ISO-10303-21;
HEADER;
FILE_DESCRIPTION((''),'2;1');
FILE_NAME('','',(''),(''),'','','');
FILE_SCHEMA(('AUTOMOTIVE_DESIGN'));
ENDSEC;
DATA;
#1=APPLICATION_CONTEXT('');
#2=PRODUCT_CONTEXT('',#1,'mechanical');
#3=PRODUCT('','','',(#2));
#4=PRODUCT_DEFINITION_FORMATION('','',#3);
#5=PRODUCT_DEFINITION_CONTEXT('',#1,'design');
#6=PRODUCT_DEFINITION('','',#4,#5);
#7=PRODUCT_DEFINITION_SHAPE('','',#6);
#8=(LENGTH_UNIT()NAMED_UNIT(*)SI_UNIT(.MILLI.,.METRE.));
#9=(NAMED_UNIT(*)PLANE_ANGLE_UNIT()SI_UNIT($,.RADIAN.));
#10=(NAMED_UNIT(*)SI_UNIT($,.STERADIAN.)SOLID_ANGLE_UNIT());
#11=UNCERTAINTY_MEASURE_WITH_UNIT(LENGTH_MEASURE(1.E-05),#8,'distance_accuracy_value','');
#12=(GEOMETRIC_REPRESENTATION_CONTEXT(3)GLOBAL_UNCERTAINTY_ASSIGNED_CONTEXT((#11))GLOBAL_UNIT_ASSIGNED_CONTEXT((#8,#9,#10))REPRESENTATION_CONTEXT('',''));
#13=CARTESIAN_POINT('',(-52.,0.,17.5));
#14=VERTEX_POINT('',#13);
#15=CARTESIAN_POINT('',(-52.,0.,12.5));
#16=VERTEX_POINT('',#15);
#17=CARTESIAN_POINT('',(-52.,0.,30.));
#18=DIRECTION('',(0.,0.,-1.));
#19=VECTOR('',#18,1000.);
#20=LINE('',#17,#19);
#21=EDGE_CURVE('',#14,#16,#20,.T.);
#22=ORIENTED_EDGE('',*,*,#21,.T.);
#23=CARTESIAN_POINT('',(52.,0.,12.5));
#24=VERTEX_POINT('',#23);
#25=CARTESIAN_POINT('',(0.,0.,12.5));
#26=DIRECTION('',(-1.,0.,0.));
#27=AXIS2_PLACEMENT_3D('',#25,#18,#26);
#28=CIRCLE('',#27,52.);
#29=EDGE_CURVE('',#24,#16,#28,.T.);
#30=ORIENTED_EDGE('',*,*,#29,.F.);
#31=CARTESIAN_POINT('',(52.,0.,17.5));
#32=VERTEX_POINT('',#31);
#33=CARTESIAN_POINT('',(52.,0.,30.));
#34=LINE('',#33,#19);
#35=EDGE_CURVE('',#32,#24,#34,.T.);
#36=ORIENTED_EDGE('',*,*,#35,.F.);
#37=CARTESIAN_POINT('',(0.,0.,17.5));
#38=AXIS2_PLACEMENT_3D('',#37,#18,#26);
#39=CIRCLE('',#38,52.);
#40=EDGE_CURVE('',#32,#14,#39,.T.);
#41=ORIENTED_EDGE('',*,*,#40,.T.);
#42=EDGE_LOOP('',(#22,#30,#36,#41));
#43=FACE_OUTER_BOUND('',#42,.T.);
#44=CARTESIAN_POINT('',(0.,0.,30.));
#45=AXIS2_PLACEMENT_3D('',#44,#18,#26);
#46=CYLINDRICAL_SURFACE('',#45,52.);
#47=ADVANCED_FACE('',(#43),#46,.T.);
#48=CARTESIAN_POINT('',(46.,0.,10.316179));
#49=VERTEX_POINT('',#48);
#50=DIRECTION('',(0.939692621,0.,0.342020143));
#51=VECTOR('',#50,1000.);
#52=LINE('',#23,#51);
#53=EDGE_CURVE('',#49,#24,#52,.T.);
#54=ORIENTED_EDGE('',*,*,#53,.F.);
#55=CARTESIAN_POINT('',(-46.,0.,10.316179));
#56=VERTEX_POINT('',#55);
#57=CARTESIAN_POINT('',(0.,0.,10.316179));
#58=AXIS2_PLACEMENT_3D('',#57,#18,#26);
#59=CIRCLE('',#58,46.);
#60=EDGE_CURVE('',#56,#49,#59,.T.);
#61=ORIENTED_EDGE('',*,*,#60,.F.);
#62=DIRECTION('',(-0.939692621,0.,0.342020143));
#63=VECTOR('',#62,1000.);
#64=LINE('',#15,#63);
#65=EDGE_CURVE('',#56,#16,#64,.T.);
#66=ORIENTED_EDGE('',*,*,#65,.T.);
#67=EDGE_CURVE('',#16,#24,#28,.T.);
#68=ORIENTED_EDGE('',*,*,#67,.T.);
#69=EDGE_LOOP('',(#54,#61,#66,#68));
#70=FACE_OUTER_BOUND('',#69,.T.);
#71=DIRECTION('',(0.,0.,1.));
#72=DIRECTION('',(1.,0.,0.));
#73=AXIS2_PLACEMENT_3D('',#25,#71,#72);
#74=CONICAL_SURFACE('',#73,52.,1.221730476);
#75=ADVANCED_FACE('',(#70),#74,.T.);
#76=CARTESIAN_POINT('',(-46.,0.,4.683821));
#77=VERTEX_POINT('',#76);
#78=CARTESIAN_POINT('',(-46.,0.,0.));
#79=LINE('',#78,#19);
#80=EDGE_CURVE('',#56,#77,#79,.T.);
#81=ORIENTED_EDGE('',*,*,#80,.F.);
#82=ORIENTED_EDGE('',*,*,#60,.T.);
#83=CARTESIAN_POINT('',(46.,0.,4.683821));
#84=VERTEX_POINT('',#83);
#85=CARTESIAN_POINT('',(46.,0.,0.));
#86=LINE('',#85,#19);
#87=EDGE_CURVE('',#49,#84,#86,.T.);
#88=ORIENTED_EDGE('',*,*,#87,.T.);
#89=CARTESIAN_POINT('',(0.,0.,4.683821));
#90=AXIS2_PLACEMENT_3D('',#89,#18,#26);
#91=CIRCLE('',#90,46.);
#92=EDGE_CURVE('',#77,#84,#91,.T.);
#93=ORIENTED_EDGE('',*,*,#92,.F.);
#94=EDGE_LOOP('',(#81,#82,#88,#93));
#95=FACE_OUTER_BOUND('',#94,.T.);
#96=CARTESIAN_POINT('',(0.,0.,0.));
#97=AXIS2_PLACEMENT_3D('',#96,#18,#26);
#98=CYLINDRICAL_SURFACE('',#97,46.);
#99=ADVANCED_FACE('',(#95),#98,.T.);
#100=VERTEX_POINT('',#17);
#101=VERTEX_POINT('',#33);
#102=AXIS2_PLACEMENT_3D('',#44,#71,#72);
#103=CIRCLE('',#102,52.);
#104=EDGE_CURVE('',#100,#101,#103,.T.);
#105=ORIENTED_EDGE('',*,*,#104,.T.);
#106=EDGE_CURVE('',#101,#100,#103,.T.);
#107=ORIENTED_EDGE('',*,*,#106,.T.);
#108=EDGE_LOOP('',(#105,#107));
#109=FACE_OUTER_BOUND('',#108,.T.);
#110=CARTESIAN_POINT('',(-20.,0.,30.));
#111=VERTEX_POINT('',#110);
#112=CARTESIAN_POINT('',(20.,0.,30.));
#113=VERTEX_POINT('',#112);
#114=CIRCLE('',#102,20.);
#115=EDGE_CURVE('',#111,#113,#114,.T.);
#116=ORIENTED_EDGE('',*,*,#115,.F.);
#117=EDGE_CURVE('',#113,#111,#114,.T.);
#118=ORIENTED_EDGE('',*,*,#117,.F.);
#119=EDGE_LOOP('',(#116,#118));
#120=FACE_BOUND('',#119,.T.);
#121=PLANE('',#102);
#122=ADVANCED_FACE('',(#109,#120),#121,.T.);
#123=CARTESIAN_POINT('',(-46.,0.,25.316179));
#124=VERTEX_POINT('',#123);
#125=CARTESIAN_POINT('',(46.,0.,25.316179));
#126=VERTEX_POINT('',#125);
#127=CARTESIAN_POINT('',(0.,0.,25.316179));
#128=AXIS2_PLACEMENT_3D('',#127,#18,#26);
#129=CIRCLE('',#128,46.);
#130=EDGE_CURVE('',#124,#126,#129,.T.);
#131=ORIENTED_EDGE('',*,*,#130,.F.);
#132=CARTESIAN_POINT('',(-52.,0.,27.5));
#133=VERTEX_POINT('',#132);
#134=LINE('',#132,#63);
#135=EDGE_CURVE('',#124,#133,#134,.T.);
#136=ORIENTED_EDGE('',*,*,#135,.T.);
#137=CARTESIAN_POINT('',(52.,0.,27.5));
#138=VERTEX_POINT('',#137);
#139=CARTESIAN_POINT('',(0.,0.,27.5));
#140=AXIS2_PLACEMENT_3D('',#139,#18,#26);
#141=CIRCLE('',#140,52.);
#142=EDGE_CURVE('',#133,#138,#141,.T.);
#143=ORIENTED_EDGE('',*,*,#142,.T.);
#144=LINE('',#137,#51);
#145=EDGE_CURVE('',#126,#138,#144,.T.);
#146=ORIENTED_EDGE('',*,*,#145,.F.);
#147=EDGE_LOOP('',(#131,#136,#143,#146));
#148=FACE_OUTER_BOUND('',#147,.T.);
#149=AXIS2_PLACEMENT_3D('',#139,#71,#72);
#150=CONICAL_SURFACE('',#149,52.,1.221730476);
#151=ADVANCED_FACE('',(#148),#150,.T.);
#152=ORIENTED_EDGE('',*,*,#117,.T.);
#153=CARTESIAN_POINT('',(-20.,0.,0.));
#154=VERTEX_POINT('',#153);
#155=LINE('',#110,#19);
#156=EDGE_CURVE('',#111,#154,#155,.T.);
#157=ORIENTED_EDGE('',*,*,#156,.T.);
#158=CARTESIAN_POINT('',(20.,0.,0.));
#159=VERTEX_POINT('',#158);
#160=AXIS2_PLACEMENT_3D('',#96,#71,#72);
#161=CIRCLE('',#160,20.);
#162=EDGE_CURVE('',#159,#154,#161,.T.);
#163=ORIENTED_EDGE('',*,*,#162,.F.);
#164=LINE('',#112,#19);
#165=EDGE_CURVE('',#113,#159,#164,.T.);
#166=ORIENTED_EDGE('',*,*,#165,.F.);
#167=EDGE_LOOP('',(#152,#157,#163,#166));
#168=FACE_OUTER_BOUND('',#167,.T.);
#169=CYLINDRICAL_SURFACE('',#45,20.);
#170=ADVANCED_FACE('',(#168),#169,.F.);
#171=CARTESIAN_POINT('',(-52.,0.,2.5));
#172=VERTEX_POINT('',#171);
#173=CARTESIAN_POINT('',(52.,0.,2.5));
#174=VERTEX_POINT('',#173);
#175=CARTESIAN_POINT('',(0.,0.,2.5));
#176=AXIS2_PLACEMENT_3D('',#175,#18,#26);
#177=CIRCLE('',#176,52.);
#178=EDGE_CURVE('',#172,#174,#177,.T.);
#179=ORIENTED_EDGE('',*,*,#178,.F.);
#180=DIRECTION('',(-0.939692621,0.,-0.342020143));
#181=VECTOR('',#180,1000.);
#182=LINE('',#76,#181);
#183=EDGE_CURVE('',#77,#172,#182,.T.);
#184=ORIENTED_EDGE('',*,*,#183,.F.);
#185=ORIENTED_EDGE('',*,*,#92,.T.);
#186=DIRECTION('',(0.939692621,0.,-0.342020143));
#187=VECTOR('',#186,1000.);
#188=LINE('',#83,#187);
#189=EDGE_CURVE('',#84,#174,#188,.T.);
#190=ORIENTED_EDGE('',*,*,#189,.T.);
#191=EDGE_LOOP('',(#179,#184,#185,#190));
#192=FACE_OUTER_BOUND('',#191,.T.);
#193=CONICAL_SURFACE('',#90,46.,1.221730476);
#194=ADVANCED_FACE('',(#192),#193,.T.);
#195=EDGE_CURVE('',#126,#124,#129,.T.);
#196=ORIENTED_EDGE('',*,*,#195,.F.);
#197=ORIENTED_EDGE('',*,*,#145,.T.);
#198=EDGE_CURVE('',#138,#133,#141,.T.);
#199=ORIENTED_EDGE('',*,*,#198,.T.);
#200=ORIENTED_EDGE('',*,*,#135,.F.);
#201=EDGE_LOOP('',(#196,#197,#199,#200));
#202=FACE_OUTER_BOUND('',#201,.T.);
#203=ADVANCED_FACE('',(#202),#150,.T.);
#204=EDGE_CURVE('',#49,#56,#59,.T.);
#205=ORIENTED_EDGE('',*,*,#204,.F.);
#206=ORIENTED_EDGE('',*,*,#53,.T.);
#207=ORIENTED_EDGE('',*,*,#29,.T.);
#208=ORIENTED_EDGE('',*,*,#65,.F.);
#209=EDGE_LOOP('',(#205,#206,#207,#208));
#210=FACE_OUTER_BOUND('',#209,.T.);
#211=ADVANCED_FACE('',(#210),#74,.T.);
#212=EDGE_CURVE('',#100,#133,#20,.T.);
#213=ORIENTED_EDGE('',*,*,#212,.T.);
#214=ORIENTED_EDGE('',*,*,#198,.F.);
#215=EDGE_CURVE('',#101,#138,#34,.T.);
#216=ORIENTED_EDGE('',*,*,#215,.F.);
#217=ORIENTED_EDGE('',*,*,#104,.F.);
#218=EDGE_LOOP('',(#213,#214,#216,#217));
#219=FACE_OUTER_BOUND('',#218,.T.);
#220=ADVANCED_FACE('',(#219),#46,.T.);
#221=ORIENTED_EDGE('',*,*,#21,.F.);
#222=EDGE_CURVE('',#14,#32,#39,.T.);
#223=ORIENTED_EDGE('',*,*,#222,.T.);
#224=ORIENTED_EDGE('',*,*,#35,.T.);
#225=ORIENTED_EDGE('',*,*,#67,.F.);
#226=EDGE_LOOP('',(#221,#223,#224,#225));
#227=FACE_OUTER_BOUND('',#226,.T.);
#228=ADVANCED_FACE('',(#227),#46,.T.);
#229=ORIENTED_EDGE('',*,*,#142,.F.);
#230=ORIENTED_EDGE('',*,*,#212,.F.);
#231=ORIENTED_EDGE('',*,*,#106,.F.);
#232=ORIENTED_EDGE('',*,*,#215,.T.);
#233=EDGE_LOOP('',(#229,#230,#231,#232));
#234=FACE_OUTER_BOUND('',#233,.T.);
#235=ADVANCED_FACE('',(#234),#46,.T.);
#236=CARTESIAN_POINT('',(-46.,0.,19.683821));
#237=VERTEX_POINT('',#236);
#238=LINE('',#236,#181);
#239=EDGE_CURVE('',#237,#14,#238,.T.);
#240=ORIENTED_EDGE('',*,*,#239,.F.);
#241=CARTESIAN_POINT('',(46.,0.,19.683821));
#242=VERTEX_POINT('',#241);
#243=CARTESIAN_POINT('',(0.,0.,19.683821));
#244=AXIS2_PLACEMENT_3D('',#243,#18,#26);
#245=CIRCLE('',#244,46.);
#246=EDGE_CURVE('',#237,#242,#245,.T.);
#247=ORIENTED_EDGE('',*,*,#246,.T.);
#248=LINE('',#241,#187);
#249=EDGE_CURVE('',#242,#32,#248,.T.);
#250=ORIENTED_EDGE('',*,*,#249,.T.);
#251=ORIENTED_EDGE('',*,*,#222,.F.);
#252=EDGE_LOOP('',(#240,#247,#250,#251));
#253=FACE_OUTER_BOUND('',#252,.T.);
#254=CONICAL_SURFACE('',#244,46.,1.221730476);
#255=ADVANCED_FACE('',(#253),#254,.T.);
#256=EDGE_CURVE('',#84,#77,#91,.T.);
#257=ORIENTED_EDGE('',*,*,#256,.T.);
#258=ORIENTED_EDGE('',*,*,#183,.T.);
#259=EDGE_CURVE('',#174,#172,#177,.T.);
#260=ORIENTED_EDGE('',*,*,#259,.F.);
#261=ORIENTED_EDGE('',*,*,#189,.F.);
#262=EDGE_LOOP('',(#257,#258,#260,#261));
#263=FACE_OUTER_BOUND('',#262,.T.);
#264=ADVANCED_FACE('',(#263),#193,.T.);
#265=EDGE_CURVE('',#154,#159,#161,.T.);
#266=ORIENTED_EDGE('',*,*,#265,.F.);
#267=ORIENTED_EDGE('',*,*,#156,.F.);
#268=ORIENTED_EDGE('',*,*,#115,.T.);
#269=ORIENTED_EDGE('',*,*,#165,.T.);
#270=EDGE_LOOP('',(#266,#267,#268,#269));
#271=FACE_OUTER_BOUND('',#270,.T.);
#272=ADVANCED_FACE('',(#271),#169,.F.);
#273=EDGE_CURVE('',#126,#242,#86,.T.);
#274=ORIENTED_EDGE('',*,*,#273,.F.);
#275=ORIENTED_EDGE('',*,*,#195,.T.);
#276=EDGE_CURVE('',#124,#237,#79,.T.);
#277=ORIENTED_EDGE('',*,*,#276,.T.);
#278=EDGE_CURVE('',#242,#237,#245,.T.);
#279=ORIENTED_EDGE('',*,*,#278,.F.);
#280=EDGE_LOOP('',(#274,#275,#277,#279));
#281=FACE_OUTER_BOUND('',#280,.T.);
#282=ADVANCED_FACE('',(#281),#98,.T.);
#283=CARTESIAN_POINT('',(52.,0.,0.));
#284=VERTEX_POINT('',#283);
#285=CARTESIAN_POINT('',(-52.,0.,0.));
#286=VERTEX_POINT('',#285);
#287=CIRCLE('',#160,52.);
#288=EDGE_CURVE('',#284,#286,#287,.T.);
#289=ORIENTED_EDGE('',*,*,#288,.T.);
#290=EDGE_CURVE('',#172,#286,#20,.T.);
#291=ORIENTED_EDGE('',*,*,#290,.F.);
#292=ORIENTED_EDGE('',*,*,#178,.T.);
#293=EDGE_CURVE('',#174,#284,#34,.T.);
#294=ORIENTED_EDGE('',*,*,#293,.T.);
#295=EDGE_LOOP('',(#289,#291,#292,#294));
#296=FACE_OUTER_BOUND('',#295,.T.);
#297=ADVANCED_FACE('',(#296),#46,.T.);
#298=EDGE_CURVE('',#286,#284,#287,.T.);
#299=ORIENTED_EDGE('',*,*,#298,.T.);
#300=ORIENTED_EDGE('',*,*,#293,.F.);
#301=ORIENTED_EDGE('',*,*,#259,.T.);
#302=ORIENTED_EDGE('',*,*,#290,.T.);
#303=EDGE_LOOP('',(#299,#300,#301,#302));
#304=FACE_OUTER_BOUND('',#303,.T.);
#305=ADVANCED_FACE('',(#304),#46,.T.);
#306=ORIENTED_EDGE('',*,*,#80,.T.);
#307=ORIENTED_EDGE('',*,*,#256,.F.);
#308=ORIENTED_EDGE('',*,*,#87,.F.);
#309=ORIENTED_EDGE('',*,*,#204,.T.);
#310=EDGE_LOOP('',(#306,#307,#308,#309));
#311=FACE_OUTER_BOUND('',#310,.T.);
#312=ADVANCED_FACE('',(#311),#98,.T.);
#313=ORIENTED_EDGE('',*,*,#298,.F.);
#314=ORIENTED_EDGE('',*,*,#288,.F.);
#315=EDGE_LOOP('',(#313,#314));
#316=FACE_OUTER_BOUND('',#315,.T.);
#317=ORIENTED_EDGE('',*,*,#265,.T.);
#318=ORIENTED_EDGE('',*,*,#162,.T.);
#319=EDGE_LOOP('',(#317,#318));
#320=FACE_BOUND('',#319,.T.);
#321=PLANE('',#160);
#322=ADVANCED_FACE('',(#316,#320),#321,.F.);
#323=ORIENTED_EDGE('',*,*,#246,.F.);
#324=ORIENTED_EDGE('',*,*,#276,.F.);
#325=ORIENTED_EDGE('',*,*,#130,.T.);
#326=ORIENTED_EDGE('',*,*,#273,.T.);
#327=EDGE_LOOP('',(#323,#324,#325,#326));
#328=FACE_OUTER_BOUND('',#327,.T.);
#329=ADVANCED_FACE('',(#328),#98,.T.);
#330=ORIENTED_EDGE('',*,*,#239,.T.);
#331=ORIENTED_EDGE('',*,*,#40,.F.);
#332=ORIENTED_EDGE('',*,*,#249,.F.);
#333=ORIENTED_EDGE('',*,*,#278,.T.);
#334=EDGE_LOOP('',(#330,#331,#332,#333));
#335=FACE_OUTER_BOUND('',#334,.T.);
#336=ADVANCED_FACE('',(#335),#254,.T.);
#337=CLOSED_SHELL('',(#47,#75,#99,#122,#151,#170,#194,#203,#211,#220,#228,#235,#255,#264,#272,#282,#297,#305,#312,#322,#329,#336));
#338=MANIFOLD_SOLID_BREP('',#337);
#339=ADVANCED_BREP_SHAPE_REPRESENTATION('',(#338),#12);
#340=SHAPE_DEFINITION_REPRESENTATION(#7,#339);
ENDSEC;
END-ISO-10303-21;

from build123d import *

# Parameters (mm, degrees)
SKETCH1_R           = 52
SKETCH1_R_2         = 20
BOSS_EXTRUDE1_DEPTH = 30


with BuildPart() as part:
    # Sketch1 → Boss-Extrude1 (new body)
    with BuildSketch(Plane.XY):
        Circle(SKETCH1_R)
        Circle(SKETCH1_R_2, mode=Mode.SUBTRACT)
    extrude(amount=BOSS_EXTRUDE1_DEPTH)

    # Sketch2 → Cut-Revolve1 (revolve, cut)
    with BuildSketch(Plane(origin=(0, 0, 0), x_dir=(0, 0, -1), z_dir=(1, 0, 0)), mode=Mode.PRIVATE) as cut_revolve1_sk:
        Polygon((-25.316178594, 46), (-19.683821406, 46), (-17.5, 52), (-27.5, 52), align=None)
        Polygon((-12.5, 52), (-10.316178594, 46), (-4.683821406, 46), (-2.5, 52), align=None)
    revolve(cut_revolve1_sk.sketch.rotate(Axis((0, 0, 0), (0, 0, 1)), 90), axis=Axis((0, 0, 0), (0, 0, 1)), mode=Mode.SUBTRACT)


solid = part.part
